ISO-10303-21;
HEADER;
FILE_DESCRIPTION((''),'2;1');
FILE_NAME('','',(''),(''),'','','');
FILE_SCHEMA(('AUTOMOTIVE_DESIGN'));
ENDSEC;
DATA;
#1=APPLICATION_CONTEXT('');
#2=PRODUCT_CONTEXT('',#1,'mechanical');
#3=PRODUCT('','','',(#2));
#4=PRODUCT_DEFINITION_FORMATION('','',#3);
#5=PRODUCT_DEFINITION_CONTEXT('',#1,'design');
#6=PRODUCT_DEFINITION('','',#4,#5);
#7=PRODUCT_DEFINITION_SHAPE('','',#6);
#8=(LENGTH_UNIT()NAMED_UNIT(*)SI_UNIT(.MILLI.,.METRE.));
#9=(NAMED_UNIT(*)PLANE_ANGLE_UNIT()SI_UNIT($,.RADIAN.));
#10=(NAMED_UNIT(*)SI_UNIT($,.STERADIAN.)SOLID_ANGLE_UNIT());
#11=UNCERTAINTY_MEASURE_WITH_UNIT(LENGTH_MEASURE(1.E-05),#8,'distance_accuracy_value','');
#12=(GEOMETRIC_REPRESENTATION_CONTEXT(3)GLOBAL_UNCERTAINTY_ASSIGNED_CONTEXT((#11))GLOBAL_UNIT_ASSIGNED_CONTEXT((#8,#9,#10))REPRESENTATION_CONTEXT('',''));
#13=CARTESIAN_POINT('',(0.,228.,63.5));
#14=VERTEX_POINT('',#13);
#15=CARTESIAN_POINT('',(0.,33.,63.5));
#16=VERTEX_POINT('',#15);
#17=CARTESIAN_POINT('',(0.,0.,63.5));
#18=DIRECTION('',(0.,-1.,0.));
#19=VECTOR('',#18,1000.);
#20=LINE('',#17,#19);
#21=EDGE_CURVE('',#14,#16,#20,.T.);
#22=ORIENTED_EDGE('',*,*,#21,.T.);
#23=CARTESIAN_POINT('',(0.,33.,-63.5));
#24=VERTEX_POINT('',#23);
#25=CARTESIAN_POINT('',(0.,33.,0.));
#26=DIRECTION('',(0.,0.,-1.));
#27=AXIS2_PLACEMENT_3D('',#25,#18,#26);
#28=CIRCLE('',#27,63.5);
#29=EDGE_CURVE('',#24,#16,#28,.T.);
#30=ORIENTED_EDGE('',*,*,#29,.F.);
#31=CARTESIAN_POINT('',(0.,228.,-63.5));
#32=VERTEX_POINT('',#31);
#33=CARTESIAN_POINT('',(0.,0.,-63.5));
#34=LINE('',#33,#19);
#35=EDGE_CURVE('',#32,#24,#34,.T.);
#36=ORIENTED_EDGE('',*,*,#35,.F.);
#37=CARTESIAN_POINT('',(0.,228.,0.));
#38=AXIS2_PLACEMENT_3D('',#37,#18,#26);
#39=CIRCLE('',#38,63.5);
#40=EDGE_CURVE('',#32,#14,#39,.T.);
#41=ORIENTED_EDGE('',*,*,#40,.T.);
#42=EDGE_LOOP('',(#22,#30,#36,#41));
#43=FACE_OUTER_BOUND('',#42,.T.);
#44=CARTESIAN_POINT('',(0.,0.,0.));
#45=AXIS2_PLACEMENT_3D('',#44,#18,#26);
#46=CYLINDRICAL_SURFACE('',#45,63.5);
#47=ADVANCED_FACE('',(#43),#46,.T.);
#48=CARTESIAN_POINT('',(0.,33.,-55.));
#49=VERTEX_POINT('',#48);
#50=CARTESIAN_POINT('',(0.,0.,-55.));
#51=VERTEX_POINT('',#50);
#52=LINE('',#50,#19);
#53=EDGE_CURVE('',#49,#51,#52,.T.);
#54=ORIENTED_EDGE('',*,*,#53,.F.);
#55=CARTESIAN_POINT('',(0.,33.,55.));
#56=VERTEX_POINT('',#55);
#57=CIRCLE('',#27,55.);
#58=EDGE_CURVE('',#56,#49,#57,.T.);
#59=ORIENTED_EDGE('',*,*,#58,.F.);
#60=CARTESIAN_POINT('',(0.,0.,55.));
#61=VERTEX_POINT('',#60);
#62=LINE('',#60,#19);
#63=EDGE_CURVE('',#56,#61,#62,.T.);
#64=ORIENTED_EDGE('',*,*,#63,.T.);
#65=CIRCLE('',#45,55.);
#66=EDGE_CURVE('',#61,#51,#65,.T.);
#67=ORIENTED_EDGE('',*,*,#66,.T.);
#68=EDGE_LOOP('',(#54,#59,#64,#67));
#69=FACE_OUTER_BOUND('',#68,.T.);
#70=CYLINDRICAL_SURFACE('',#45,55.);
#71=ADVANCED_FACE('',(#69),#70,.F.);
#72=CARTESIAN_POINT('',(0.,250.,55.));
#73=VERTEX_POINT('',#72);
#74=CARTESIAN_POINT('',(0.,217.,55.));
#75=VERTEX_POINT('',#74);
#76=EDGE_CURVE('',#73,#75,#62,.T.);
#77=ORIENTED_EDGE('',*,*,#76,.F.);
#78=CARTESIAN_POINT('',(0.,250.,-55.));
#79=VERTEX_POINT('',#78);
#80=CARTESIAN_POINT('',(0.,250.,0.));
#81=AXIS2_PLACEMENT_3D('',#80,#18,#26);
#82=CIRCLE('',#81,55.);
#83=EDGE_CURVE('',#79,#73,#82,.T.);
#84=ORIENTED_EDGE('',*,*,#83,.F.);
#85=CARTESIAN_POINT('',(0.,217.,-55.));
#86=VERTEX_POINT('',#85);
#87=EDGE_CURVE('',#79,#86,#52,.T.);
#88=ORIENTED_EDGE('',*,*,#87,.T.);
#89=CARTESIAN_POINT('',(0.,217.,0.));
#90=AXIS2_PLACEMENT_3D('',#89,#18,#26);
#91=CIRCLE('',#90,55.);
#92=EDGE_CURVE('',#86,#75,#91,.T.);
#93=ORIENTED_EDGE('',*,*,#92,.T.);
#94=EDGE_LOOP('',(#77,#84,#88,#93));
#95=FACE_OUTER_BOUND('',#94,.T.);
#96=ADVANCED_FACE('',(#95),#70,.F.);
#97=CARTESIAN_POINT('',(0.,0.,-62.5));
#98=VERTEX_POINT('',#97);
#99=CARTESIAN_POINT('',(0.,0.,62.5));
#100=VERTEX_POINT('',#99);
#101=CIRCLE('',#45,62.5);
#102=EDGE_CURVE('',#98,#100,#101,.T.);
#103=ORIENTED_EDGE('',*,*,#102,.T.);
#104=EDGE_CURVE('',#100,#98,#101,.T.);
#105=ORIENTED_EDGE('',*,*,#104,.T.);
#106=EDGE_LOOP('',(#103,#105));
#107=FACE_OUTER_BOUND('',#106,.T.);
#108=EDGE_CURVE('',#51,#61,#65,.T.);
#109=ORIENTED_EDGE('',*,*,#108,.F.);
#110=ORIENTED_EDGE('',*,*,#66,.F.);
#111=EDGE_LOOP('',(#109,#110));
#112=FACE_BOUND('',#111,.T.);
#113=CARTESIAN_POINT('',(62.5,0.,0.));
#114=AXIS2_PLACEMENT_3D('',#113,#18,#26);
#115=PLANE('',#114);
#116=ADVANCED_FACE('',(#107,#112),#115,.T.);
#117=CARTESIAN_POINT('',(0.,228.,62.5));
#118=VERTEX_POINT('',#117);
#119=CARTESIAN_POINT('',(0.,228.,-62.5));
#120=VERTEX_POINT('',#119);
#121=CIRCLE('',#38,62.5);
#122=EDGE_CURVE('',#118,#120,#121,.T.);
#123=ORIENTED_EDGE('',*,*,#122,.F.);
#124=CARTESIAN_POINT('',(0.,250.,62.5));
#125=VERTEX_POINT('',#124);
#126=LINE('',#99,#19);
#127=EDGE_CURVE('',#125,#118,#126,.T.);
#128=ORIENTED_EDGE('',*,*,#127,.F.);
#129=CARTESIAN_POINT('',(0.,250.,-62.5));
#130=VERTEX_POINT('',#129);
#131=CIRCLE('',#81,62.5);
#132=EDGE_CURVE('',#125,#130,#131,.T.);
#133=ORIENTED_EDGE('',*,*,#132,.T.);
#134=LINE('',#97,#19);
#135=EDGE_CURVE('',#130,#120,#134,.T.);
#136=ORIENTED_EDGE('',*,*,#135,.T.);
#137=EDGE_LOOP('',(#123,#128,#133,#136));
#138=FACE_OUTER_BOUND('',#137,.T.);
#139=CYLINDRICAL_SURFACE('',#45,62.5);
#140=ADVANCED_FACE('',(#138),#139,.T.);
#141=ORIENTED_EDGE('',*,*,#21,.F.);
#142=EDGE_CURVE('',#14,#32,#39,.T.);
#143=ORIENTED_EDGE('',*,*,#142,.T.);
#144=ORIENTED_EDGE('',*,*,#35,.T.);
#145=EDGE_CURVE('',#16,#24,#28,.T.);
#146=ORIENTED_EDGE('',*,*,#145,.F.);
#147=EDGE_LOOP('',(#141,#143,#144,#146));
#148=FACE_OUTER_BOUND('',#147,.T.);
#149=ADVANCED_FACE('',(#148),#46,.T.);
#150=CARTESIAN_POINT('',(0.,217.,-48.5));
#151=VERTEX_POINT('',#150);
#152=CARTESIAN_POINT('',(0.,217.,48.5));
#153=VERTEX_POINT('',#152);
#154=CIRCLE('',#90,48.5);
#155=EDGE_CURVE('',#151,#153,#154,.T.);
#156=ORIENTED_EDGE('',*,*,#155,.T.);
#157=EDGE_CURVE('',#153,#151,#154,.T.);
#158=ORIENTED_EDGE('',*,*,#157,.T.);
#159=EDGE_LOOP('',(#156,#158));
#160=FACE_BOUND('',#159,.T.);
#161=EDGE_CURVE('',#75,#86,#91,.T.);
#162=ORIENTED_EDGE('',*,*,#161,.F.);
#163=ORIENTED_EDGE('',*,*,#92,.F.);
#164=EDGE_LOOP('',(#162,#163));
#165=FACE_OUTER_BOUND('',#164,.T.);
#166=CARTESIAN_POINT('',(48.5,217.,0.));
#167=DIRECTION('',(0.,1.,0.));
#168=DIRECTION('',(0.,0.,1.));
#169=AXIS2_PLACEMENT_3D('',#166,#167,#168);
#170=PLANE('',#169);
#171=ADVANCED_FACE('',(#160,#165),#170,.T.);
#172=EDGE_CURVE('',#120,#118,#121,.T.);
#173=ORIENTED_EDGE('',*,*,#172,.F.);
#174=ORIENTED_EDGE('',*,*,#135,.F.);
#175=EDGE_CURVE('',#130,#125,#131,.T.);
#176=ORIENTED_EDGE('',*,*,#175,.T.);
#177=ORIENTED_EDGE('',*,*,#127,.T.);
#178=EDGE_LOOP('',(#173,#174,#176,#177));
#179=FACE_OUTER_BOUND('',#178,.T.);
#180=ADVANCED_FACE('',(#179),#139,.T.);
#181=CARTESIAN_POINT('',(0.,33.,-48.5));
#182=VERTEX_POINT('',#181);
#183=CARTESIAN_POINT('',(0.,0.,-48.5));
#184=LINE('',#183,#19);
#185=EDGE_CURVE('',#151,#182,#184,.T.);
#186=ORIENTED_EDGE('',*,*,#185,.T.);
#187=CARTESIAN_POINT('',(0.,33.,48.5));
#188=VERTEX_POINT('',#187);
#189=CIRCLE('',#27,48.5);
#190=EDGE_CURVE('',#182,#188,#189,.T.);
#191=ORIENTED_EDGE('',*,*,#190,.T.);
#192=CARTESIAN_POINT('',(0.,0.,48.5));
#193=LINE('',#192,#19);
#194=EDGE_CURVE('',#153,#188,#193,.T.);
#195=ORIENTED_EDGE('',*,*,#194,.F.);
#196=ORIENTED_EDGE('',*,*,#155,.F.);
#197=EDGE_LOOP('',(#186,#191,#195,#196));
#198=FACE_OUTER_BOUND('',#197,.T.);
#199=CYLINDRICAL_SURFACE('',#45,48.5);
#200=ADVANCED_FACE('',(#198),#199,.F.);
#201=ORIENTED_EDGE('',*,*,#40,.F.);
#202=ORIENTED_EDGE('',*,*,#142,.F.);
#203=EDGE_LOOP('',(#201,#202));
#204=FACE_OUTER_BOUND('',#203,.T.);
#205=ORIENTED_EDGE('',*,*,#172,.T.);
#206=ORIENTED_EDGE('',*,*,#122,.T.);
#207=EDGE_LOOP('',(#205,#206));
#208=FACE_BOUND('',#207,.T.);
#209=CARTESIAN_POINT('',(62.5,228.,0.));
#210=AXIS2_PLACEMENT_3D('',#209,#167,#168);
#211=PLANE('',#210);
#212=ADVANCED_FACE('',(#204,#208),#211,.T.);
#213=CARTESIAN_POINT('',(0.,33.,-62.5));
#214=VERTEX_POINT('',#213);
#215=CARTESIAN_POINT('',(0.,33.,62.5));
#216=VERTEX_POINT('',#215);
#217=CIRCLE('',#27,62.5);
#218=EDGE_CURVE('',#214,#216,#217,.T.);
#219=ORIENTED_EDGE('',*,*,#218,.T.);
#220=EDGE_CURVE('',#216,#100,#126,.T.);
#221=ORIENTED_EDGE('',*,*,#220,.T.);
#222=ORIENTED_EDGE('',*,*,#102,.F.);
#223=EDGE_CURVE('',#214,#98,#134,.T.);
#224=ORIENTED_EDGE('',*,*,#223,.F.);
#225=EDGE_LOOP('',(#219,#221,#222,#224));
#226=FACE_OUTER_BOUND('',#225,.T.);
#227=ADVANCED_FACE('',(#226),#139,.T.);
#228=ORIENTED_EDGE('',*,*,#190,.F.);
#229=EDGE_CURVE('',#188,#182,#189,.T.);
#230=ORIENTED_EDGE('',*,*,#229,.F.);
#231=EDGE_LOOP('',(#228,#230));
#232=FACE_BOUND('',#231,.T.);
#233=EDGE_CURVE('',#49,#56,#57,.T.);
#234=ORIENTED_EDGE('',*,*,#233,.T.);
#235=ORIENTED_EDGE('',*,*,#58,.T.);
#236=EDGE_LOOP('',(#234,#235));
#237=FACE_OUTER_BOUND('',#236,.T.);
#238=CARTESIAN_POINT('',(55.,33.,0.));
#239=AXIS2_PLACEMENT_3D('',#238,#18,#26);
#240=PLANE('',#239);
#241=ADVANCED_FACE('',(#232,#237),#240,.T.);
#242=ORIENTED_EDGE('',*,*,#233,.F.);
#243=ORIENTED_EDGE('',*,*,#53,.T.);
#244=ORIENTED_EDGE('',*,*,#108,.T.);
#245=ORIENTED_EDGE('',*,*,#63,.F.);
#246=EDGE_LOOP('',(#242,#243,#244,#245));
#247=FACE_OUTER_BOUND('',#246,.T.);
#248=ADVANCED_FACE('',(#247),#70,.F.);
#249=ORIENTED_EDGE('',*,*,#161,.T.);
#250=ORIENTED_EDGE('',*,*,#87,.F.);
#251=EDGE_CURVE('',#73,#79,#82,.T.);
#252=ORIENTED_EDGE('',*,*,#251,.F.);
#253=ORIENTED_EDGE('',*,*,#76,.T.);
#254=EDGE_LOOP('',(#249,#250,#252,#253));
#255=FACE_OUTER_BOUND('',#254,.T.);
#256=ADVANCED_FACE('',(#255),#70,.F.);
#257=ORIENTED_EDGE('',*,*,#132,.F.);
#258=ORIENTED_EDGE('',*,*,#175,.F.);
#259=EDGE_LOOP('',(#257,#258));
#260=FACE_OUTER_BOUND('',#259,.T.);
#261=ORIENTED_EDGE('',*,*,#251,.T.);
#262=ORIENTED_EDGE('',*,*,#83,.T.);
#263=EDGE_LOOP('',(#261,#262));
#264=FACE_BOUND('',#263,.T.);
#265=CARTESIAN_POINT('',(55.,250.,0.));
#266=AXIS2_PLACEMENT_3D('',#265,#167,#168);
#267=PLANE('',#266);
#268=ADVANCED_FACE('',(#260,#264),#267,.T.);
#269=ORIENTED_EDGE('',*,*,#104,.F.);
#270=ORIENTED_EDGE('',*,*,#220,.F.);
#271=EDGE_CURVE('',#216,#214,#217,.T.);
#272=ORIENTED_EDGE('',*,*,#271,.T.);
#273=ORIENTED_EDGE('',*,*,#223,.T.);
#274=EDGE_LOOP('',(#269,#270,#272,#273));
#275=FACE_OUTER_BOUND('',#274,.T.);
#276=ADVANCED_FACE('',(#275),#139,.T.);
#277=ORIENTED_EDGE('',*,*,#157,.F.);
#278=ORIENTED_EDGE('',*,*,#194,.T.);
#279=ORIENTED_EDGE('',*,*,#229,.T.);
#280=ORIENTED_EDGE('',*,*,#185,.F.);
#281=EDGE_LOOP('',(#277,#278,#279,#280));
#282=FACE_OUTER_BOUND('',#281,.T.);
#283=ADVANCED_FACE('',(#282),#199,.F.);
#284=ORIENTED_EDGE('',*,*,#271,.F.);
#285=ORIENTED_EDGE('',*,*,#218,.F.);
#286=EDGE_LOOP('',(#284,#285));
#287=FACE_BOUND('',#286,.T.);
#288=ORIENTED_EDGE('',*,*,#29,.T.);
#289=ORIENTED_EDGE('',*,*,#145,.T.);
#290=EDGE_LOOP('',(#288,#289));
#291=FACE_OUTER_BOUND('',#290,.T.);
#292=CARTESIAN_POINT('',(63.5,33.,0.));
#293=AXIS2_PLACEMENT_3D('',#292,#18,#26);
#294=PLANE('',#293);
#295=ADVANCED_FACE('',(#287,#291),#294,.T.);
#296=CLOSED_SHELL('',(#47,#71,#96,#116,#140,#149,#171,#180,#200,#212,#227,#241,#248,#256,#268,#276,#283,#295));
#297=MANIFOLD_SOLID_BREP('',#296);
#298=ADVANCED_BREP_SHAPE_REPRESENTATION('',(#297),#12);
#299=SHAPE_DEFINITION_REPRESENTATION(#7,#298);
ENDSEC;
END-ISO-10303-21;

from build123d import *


with BuildPart() as part:
    # Sketch1 → Revolve1 (revolve)
    with BuildSketch(Plane.XY, mode=Mode.PRIVATE) as revolve1_sk:
        Polygon((55, 0), (55, 33), (48.5, 33), (48.5, 217), (55, 217), (55, 250), (62.5, 250), (62.5, 228), (63.5, 228), (63.5, 33), (62.5, 33), (62.5, 0), align=None)
    revolve(revolve1_sk.sketch.rotate(Axis((0, 0, 0), (0, 1, 0)), 90), axis=Axis((0, 0, 0), (0, 1, 0)))


solid = part.part
